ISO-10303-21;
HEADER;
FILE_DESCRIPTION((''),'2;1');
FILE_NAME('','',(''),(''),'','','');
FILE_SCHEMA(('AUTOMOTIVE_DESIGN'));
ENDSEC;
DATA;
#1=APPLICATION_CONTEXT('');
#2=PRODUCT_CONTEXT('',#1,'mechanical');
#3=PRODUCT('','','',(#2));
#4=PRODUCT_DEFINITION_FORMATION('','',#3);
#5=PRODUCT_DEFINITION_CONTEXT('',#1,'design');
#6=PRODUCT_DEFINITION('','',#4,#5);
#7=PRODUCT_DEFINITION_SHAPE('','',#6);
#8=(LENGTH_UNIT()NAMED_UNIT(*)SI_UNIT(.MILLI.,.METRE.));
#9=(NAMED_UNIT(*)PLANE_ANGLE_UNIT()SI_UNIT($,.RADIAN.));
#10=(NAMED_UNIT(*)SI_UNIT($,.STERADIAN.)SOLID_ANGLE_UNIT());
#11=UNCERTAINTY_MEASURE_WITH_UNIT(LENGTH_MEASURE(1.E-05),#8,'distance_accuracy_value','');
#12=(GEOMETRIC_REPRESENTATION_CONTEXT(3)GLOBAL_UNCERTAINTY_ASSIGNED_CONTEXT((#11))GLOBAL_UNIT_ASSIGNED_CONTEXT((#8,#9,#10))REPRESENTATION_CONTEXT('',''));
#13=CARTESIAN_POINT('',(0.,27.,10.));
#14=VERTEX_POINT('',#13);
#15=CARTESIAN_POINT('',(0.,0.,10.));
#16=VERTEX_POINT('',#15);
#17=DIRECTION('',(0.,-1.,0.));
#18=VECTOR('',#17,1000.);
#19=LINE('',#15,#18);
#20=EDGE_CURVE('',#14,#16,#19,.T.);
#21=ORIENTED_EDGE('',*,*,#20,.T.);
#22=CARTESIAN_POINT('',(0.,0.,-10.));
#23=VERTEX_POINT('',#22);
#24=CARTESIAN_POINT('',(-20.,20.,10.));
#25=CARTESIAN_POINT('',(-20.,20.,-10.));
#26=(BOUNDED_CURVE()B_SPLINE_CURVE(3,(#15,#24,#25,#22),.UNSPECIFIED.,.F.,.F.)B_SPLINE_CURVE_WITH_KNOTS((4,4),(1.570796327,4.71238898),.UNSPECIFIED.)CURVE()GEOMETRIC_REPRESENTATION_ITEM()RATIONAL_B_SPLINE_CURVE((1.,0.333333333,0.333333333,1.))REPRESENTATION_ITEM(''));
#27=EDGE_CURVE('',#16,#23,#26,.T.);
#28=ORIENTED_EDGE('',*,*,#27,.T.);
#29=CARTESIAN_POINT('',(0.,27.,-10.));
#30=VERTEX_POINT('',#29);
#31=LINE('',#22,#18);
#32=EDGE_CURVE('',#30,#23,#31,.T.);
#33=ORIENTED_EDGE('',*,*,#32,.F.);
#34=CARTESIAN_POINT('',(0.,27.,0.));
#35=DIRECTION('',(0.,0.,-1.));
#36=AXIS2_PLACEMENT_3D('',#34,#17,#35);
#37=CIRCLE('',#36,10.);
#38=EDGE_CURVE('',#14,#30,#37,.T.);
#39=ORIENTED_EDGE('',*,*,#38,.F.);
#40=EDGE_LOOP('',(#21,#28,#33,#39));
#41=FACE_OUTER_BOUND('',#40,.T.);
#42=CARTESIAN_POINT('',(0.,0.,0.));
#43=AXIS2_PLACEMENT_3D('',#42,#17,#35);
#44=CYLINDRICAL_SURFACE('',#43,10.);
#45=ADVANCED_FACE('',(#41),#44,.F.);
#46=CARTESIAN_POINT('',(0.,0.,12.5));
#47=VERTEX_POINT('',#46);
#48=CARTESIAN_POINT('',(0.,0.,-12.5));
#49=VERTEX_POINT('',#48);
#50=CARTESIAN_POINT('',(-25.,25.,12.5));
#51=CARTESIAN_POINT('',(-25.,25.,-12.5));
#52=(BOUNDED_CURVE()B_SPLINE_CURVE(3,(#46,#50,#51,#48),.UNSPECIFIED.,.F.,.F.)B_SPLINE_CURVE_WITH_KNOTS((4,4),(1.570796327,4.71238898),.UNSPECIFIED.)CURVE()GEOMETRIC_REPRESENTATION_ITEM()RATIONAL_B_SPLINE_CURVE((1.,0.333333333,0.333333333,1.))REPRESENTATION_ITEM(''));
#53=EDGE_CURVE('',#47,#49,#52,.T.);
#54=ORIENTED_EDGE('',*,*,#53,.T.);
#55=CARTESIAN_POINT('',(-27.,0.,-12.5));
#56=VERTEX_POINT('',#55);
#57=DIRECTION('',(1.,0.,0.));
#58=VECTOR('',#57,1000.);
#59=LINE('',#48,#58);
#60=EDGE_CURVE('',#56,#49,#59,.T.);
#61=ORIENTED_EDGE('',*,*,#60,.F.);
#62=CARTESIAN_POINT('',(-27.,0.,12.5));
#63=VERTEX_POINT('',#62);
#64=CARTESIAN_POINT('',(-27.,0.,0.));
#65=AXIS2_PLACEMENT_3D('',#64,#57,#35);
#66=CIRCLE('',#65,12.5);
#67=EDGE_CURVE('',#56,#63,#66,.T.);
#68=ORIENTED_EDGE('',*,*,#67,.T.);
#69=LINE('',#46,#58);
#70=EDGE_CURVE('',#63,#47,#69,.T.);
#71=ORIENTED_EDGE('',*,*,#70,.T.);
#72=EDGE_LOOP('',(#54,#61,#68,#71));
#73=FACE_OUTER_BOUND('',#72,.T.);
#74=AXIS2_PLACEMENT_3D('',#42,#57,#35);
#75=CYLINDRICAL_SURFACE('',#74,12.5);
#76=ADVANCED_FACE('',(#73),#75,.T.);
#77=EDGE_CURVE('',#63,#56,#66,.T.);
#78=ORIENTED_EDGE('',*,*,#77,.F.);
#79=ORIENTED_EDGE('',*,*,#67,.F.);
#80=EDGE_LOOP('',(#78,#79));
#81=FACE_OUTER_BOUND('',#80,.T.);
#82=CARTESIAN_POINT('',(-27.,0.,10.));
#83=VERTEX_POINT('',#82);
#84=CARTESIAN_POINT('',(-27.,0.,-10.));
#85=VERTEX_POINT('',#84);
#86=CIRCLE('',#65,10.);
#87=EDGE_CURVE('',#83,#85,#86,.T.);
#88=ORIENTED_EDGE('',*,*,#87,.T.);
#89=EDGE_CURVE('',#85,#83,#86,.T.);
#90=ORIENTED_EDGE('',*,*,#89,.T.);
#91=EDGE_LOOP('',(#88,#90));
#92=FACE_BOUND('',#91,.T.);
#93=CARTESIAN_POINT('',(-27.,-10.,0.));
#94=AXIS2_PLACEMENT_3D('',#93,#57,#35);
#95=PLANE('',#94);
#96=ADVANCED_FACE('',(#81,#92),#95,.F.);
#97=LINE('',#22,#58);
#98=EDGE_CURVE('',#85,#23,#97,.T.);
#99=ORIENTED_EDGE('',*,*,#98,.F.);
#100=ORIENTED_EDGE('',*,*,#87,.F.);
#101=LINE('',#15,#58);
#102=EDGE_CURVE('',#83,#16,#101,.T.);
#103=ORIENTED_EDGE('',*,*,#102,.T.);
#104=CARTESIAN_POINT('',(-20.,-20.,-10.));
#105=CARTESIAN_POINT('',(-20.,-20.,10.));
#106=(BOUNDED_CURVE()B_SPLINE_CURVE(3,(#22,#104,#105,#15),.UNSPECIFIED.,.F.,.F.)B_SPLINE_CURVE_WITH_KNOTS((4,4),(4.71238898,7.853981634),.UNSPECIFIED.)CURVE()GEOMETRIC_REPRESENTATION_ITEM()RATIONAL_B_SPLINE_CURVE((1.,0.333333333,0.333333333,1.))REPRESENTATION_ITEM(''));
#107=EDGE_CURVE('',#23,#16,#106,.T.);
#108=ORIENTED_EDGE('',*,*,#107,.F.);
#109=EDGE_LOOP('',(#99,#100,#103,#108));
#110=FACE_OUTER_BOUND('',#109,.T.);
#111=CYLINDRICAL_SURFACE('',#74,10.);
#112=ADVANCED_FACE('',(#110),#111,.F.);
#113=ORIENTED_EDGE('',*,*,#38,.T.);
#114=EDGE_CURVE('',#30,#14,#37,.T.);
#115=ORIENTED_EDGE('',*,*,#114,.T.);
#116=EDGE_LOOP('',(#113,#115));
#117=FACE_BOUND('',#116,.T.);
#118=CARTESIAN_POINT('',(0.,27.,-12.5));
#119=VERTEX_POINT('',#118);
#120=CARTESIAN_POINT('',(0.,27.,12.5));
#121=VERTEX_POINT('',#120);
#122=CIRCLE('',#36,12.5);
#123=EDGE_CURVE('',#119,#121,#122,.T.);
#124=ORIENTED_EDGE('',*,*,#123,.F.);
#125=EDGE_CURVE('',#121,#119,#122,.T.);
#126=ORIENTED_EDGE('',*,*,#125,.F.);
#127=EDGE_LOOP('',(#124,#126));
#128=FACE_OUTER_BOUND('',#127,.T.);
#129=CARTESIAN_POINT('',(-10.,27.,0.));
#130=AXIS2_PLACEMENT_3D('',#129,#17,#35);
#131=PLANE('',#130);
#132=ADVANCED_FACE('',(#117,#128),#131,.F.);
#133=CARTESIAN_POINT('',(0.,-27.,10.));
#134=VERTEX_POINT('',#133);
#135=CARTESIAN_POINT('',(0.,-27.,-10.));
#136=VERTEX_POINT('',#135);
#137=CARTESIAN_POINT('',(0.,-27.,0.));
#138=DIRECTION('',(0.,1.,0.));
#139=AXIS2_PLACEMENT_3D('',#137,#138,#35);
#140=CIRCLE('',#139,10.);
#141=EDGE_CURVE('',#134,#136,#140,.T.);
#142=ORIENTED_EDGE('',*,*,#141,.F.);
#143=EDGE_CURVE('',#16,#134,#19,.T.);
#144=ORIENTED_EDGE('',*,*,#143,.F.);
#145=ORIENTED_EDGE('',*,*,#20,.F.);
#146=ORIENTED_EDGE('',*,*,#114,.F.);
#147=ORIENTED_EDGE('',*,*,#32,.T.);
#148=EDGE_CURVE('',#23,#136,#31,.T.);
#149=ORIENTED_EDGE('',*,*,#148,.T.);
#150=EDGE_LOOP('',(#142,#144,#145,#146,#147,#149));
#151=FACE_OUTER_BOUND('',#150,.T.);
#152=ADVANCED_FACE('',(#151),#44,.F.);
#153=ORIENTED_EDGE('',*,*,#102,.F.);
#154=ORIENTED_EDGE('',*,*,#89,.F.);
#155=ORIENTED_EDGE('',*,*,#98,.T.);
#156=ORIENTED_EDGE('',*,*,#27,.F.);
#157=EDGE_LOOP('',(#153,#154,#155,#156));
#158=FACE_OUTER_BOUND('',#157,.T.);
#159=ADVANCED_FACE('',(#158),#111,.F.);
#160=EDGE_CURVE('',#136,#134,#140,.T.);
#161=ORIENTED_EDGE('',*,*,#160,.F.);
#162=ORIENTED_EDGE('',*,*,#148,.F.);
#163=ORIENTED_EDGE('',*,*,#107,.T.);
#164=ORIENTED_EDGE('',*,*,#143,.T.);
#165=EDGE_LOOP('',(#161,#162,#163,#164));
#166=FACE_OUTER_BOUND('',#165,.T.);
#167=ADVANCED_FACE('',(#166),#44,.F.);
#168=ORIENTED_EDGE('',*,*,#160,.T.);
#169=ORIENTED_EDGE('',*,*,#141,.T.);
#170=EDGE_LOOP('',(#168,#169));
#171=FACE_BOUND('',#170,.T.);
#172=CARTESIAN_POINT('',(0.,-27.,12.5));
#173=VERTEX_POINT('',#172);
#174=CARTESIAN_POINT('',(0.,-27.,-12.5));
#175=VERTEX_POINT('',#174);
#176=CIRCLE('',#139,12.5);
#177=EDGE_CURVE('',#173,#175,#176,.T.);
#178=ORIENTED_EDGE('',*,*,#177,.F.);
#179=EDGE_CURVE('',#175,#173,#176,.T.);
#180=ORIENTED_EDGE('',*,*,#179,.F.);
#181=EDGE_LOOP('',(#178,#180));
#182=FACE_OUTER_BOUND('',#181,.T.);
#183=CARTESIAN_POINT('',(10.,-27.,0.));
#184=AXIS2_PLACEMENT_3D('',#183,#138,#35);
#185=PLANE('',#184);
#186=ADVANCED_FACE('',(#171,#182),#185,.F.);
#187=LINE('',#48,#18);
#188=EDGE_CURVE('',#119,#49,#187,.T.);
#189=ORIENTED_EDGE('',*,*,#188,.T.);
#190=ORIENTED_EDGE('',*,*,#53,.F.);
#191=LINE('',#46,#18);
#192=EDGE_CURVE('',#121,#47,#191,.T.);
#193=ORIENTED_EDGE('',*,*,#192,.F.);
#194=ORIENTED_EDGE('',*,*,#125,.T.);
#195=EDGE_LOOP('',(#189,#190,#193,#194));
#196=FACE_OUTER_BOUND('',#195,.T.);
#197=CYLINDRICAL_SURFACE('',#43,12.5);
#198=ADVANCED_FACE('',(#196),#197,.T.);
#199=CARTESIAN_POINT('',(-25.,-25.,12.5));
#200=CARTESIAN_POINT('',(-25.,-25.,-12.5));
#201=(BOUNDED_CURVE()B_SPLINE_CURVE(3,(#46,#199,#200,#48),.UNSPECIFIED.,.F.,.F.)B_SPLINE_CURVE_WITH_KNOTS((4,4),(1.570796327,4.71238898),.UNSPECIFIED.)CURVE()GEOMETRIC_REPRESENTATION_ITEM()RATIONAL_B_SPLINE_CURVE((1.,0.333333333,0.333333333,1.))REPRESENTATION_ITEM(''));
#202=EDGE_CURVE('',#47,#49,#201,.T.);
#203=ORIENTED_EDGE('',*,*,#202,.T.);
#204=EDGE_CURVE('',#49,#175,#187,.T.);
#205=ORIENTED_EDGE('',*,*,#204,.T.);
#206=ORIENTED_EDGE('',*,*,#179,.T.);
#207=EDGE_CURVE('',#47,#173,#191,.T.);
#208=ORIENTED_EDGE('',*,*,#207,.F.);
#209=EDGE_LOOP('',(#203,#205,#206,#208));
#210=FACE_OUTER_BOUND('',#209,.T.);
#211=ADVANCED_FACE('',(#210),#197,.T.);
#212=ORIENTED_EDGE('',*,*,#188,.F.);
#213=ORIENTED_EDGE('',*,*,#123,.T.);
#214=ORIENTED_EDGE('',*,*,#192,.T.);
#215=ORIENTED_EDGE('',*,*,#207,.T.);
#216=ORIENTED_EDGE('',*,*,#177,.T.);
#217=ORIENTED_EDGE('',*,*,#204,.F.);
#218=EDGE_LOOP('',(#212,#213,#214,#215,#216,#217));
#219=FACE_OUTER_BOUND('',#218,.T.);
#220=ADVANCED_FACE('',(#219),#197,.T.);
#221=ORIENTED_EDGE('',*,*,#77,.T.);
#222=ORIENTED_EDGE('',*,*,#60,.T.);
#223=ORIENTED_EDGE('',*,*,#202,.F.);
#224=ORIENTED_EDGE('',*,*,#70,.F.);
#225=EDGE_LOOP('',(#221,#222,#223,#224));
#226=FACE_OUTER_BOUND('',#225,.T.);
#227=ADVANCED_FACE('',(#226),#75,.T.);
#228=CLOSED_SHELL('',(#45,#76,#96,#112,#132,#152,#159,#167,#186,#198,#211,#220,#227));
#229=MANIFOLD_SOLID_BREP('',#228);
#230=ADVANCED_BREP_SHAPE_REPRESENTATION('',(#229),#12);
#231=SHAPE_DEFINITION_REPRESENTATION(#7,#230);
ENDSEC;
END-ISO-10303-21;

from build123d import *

# Parameters (mm, degrees)
SKETCH_1_W               = 2.5
SKETCH_1_H               = 27
PATTERN_CIRCULAR_1_COUNT = 3
PATTERN_CIRCULAR_1_ANGLE = 180
SKETCH_2_R               = 10
CUT_EXTRUDE_1_DEPTH      = 62.654278166
SKETCH_3_R               = 10
CUT_EXTRUDE_2_DEPTH      = 41.177730217


with BuildPart() as part:
    # 草图1 → 旋转1 (revolve)
    with BuildSketch(Plane.XY, mode=Mode.PRIVATE) as revolve_1_sk:
        with Locations((-11.25, 13.5)):
            Rectangle(SKETCH_1_W, SKETCH_1_H)
    revolve_1 = revolve(revolve_1_sk.sketch.rotate(Axis((0, 0, 0), (0, 1, 0)), 270), axis=Axis((0, 0, 0), (0, 1, 0)))

    # 阵列(圆周)1: 旋转1 ×3 about axis
    pattern_circular_1_axis = Axis((0, 0, 0), (0, 0, 1))
    for i in range(1, PATTERN_CIRCULAR_1_COUNT):
        add(revolve_1.rotate(pattern_circular_1_axis, i * PATTERN_CIRCULAR_1_ANGLE / (PATTERN_CIRCULAR_1_COUNT - 1)))

    # 草图2 → 切除-拉伸1 (cut, through all)
    with BuildSketch(Plane.XZ.offset(27)):
        with Locations(Location((0, 0, 0), (0, 0, 270))):
            Circle(SKETCH_2_R)
    extrude(amount=-CUT_EXTRUDE_1_DEPTH, mode=Mode.SUBTRACT)

    # 草图3 → 切除-拉伸2 (cut, through all)
    with BuildSketch(Plane(origin=(0, 0, 0), x_dir=(0, 0, -1), z_dir=(1, 0, 0))):
        Circle(SKETCH_3_R)
    extrude(amount=-CUT_EXTRUDE_2_DEPTH, mode=Mode.SUBTRACT)


solid = part.part
